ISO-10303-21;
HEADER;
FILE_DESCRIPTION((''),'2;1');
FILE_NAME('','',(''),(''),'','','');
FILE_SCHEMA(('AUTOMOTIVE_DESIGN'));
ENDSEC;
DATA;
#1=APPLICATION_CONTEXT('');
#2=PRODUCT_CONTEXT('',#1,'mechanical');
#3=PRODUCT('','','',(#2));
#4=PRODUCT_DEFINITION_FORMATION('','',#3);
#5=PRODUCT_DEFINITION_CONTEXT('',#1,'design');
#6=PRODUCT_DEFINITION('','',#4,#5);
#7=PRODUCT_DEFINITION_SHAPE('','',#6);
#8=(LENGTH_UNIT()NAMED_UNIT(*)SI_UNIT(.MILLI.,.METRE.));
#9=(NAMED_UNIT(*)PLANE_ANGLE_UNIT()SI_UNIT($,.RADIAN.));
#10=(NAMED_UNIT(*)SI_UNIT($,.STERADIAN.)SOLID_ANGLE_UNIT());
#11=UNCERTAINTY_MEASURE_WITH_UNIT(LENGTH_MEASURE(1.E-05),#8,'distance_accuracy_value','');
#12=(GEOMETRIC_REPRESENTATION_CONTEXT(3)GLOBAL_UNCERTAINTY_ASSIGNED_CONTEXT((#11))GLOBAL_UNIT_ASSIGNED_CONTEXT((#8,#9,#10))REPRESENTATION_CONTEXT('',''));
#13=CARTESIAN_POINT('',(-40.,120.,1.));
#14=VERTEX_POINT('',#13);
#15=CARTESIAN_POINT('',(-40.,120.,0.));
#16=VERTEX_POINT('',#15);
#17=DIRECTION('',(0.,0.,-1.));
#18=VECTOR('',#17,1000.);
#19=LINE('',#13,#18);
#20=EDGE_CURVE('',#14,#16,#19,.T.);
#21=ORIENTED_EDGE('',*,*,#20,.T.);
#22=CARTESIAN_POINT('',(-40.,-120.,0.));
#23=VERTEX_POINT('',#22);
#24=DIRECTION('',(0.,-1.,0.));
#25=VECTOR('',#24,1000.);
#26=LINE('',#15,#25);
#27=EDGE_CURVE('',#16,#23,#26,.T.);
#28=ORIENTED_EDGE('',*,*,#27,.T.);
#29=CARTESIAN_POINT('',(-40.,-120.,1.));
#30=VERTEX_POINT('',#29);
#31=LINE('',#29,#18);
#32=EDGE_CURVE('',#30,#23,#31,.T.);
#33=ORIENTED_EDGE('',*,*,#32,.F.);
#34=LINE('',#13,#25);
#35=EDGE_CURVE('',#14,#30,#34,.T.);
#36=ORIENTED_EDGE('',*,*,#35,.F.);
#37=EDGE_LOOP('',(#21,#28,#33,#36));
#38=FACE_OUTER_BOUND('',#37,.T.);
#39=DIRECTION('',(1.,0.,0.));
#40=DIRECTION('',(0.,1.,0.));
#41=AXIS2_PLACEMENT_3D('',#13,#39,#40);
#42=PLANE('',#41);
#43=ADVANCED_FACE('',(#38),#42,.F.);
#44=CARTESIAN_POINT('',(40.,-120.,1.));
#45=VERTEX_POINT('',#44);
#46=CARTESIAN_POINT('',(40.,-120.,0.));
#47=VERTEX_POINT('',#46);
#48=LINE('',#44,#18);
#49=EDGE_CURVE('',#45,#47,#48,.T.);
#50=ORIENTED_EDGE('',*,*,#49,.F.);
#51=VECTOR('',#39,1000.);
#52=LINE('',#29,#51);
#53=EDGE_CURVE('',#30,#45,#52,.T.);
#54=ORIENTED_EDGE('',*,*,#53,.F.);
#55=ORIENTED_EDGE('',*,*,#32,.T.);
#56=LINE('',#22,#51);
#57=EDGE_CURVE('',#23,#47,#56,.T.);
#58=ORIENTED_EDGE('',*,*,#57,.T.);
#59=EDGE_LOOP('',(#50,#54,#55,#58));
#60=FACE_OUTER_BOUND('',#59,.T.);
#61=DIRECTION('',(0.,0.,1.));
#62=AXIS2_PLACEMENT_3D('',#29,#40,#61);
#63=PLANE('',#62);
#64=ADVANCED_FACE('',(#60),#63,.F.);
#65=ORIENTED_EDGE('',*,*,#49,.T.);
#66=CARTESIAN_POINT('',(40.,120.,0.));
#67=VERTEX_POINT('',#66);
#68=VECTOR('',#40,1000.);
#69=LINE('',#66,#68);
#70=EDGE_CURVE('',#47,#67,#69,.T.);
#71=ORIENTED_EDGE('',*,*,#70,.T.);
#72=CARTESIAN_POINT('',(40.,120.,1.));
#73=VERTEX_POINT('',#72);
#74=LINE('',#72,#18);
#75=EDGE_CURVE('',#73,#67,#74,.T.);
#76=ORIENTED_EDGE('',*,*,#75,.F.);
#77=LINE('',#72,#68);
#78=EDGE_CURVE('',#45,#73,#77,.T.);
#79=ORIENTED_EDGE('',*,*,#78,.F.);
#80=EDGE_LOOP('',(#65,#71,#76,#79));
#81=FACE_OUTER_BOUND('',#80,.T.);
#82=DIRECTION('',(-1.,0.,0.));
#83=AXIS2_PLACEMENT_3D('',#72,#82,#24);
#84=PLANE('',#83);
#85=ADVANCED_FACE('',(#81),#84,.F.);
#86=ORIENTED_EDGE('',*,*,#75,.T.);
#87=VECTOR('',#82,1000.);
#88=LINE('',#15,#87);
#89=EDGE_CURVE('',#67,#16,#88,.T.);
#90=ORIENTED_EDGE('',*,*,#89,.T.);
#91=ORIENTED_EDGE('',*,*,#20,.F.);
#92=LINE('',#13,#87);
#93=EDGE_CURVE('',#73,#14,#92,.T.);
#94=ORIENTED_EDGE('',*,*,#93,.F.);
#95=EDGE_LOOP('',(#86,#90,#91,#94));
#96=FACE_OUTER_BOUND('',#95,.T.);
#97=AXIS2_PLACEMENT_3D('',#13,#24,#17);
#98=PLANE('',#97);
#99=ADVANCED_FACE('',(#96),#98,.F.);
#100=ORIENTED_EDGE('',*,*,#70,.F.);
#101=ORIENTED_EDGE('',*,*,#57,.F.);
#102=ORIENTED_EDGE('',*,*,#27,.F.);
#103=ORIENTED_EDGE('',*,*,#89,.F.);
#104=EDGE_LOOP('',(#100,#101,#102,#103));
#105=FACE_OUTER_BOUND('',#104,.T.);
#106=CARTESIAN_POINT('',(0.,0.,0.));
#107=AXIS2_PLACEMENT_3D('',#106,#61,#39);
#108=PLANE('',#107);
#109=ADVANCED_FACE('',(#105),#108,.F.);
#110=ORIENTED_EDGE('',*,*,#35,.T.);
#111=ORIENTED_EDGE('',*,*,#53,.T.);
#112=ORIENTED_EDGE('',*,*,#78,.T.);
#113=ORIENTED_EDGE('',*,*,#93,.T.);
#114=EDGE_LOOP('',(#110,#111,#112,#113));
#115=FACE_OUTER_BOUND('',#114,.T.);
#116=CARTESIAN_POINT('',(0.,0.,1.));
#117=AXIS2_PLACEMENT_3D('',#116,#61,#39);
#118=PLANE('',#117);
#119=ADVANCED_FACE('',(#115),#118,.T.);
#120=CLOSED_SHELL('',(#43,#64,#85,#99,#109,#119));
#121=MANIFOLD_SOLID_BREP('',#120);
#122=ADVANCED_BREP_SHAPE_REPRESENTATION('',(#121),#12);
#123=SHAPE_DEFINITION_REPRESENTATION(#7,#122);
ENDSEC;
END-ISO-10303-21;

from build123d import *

# Parameters (mm, degrees)
SKETCH1_W           = 80
SKETCH1_H           = 240
BOSS_EXTRUDE1_DEPTH = 1


with BuildPart() as part:
    # Sketch1 → Boss-Extrude1 (new body)
    with BuildSketch(Plane.XY):
        Rectangle(SKETCH1_W, SKETCH1_H)
    extrude(amount=BOSS_EXTRUDE1_DEPTH)


solid = part.part
